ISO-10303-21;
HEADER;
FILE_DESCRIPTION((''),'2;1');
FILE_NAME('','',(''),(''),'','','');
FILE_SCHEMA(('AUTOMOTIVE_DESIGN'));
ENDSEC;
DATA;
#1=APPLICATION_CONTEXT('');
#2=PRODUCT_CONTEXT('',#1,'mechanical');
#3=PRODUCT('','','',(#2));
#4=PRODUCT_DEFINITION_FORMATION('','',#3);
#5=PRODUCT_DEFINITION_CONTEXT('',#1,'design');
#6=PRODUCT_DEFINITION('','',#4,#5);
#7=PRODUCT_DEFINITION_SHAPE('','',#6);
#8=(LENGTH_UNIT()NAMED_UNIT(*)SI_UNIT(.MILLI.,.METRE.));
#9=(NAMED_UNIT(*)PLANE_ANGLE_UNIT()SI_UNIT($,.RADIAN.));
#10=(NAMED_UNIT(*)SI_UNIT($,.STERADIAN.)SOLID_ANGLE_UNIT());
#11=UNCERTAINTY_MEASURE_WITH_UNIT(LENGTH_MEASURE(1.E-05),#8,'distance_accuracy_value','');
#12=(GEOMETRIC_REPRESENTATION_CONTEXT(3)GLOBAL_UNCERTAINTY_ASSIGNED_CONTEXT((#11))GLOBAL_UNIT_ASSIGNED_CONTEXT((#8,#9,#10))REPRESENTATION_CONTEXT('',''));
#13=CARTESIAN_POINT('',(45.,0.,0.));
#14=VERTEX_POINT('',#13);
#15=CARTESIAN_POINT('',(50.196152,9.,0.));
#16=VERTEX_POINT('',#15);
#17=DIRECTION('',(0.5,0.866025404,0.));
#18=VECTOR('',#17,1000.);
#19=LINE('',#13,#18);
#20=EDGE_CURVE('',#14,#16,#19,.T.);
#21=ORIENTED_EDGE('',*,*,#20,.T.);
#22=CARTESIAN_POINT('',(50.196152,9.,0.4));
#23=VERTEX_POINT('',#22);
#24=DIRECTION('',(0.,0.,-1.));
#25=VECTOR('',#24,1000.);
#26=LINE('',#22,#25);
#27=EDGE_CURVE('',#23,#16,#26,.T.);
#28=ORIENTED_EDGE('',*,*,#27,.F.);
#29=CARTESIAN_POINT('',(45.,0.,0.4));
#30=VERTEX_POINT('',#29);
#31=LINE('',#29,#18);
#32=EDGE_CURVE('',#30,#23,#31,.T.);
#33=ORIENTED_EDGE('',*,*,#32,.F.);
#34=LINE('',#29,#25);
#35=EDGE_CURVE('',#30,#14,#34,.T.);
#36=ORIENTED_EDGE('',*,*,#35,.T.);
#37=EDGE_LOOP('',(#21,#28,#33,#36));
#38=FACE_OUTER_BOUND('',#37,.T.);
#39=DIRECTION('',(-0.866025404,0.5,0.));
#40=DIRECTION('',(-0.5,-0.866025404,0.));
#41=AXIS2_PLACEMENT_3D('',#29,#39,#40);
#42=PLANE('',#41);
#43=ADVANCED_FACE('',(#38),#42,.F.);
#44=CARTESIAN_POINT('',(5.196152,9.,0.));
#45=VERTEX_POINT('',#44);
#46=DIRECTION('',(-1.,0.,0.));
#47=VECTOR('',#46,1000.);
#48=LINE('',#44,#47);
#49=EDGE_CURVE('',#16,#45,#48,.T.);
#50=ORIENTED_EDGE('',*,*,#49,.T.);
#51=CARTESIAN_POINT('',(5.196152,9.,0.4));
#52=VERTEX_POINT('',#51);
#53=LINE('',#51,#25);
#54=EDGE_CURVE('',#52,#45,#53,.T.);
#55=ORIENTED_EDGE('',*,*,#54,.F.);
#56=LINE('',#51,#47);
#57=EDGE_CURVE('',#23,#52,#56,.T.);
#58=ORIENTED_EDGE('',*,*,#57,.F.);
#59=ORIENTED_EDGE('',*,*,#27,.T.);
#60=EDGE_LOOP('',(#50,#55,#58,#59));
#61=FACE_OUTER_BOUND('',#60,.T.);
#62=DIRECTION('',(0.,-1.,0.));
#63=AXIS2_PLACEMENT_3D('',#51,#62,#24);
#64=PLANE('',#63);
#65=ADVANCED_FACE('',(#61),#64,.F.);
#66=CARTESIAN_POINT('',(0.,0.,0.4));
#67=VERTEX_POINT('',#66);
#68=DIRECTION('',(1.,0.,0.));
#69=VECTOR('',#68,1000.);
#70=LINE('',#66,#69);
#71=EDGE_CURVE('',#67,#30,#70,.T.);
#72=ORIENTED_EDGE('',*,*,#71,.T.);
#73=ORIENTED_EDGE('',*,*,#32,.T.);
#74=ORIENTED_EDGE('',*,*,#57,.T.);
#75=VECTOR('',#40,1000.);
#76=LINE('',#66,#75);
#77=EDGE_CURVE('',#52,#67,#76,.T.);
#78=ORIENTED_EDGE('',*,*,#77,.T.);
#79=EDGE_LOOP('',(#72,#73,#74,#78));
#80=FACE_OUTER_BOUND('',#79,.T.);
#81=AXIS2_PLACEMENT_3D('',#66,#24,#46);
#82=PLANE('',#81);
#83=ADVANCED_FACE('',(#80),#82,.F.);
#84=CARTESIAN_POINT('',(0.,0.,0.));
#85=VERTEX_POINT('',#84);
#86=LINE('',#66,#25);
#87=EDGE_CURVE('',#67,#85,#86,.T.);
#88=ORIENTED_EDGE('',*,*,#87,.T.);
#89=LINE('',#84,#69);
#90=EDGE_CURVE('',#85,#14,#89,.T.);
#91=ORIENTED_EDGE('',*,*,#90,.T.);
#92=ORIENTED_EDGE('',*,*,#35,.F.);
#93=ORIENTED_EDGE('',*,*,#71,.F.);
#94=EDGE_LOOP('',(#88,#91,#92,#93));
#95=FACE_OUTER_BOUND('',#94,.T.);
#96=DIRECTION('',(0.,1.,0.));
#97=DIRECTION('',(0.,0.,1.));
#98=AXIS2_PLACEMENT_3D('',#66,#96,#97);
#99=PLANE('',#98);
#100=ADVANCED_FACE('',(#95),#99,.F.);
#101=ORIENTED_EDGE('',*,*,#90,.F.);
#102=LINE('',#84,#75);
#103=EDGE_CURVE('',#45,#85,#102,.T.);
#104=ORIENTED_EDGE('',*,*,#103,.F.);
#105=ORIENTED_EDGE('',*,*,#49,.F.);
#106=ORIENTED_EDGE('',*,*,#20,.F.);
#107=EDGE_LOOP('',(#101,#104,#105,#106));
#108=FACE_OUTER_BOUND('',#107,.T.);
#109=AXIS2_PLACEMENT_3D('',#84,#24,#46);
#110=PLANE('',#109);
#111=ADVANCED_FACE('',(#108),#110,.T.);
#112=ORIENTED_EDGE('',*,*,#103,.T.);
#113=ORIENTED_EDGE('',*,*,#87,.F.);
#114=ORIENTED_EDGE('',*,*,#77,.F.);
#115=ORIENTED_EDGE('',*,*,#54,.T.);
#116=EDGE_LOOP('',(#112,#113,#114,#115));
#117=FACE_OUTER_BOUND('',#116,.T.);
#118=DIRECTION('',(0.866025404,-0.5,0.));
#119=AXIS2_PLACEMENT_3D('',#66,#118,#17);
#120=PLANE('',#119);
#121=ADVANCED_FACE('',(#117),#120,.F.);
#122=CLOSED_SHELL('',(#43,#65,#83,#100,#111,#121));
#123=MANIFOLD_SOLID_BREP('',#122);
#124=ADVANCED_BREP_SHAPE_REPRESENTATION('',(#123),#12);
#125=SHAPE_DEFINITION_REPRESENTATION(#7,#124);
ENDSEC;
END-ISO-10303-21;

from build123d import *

# Parameters (mm, degrees)
BOSS_EXTRUDE1_DEPTH = 0.4


with BuildPart() as part:
    # Sketch1 → Boss-Extrude1 (new body)
    with BuildSketch(Plane.XY):
        Polygon((0, 0), (45, 0), (50.196152423, 9), (5.196152423, 9), align=None)
    extrude(amount=BOSS_EXTRUDE1_DEPTH)


solid = part.part
